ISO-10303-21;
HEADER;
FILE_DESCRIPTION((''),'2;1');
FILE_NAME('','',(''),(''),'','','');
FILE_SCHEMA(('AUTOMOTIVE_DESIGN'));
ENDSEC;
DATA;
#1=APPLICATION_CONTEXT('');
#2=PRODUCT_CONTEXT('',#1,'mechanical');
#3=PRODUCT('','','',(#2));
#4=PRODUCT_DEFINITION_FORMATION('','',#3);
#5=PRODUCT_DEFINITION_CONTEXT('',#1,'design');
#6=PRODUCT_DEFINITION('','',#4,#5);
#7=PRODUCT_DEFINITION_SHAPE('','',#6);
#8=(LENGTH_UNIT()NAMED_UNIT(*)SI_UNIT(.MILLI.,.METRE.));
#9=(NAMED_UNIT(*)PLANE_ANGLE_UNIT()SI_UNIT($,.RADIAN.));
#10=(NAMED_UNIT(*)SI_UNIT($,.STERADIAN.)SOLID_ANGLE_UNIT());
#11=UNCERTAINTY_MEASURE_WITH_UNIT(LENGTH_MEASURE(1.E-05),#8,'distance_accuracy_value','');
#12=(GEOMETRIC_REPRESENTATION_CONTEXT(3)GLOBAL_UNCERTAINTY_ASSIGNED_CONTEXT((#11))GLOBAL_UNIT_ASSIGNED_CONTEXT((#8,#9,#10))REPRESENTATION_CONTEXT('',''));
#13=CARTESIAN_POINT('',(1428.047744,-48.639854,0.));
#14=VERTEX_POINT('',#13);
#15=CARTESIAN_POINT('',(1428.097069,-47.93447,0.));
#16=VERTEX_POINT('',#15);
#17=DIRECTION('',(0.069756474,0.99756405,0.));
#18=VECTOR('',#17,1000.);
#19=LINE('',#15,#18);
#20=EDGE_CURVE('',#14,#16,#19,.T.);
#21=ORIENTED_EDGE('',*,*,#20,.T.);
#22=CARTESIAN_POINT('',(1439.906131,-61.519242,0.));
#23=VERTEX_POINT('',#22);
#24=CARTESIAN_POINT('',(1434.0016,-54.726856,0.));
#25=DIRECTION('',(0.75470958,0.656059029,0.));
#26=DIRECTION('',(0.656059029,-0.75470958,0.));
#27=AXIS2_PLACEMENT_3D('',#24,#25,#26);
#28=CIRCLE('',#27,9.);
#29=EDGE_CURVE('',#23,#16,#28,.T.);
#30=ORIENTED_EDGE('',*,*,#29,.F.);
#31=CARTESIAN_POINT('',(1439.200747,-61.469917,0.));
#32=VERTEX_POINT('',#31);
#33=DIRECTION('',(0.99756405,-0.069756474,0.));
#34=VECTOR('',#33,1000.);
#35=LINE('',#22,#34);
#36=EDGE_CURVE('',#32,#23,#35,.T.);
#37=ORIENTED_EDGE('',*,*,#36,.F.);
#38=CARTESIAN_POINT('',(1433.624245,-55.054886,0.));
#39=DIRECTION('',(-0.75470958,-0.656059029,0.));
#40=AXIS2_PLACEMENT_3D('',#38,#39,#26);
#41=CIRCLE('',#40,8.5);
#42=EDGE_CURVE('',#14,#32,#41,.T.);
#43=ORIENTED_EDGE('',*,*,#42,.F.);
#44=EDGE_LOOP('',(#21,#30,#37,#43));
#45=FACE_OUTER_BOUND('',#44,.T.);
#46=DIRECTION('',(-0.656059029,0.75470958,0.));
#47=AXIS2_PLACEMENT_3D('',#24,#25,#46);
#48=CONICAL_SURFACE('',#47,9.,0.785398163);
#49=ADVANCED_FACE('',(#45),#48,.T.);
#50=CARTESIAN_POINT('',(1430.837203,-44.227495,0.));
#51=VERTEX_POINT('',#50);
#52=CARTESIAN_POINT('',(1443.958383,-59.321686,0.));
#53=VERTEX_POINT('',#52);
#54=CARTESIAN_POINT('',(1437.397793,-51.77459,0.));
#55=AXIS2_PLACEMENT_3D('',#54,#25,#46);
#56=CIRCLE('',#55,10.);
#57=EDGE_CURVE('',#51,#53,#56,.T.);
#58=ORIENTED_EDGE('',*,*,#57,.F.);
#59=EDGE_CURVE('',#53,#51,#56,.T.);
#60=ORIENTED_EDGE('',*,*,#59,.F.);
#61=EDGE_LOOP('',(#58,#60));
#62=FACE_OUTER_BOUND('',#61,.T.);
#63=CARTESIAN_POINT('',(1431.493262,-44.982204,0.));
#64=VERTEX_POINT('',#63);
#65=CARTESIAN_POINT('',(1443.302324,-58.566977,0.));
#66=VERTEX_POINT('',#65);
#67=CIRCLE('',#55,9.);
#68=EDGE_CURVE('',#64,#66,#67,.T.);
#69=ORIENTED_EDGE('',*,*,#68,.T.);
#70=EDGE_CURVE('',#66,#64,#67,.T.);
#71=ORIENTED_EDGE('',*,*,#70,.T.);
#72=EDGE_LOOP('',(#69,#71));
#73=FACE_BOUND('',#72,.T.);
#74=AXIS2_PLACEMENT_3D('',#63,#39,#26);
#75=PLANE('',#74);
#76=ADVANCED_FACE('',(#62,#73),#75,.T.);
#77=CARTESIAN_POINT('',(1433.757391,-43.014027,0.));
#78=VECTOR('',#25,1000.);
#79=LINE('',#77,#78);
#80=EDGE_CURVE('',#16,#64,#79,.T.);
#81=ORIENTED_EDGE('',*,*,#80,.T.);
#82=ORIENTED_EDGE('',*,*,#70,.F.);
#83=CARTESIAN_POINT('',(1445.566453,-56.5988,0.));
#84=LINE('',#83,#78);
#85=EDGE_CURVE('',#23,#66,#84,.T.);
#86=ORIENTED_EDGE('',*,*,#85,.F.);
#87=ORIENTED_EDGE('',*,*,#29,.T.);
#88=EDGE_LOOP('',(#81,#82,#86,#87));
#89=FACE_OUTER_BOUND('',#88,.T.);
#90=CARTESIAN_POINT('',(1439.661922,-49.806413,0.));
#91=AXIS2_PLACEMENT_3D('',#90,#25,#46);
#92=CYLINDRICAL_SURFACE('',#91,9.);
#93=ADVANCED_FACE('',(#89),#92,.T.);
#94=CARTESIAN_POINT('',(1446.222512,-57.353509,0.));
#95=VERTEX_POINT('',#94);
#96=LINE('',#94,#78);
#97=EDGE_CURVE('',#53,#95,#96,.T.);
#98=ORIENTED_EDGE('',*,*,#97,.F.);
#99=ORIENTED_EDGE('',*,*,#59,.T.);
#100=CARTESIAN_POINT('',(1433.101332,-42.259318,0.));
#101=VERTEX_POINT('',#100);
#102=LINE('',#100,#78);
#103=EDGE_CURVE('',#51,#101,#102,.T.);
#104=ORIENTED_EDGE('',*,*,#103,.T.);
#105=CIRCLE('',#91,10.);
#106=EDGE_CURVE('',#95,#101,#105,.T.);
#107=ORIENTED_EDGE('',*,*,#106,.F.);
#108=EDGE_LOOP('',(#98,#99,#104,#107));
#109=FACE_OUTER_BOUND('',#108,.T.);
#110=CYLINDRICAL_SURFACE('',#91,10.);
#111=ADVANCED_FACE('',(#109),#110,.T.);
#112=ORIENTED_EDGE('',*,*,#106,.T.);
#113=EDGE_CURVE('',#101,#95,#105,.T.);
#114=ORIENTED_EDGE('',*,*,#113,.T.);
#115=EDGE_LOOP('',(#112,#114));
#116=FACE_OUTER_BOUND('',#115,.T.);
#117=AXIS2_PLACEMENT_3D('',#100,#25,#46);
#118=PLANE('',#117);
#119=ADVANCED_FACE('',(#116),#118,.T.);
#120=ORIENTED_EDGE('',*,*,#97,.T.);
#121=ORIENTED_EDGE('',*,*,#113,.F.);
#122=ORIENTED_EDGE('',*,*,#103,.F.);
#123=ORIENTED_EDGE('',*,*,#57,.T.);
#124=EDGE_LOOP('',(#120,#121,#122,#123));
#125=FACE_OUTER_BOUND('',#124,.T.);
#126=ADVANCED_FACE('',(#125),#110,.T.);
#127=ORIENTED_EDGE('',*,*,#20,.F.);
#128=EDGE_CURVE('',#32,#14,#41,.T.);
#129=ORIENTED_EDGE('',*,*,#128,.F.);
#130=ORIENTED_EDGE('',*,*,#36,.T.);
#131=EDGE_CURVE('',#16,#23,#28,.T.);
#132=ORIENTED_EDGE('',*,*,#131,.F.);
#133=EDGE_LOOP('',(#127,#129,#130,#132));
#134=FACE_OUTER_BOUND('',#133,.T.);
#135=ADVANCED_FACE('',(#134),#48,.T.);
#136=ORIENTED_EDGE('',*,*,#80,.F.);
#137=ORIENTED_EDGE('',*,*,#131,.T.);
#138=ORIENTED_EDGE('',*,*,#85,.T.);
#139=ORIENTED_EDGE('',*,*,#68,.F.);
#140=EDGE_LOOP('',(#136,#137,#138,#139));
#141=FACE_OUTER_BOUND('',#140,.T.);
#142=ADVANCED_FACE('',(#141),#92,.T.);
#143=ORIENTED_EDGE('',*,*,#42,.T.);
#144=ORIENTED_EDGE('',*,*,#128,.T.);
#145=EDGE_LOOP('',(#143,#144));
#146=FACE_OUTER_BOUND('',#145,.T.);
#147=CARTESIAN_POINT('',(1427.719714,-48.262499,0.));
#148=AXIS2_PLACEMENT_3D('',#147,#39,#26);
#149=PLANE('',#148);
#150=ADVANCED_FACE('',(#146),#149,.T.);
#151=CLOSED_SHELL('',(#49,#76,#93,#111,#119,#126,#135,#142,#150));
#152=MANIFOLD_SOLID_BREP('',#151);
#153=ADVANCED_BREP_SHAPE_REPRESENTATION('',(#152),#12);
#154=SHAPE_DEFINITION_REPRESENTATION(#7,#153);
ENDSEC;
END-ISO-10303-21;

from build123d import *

# Parameters (mm, degrees)
CHAMFER1_SIZE = 0.5


with BuildPart() as part:
    # Sketch1 → Revolve1 (revolve)
    with BuildSketch(Plane.XY):
        Polygon((1431.493261903, -44.982204273), (1430.837202874, -44.227494693), (1433.101331614, -42.259317606), (1439.661921904, -49.806413409), (1433.624245262, -55.05488564), (1427.719714002, -48.262499418), align=None)
    revolve(axis=Axis((1439.661921904, -49.806413409, 0), (-0.7547095802227773, -0.6560590289905012, 0)))

    # Chamfer1
    chamfer1_edges = [part.edges().sort_by_distance(p)[0] for p in [
        (1439.528776523, -61.847271862, 0),
    ]]
    chamfer(chamfer1_edges, length=CHAMFER1_SIZE)


solid = part.part
